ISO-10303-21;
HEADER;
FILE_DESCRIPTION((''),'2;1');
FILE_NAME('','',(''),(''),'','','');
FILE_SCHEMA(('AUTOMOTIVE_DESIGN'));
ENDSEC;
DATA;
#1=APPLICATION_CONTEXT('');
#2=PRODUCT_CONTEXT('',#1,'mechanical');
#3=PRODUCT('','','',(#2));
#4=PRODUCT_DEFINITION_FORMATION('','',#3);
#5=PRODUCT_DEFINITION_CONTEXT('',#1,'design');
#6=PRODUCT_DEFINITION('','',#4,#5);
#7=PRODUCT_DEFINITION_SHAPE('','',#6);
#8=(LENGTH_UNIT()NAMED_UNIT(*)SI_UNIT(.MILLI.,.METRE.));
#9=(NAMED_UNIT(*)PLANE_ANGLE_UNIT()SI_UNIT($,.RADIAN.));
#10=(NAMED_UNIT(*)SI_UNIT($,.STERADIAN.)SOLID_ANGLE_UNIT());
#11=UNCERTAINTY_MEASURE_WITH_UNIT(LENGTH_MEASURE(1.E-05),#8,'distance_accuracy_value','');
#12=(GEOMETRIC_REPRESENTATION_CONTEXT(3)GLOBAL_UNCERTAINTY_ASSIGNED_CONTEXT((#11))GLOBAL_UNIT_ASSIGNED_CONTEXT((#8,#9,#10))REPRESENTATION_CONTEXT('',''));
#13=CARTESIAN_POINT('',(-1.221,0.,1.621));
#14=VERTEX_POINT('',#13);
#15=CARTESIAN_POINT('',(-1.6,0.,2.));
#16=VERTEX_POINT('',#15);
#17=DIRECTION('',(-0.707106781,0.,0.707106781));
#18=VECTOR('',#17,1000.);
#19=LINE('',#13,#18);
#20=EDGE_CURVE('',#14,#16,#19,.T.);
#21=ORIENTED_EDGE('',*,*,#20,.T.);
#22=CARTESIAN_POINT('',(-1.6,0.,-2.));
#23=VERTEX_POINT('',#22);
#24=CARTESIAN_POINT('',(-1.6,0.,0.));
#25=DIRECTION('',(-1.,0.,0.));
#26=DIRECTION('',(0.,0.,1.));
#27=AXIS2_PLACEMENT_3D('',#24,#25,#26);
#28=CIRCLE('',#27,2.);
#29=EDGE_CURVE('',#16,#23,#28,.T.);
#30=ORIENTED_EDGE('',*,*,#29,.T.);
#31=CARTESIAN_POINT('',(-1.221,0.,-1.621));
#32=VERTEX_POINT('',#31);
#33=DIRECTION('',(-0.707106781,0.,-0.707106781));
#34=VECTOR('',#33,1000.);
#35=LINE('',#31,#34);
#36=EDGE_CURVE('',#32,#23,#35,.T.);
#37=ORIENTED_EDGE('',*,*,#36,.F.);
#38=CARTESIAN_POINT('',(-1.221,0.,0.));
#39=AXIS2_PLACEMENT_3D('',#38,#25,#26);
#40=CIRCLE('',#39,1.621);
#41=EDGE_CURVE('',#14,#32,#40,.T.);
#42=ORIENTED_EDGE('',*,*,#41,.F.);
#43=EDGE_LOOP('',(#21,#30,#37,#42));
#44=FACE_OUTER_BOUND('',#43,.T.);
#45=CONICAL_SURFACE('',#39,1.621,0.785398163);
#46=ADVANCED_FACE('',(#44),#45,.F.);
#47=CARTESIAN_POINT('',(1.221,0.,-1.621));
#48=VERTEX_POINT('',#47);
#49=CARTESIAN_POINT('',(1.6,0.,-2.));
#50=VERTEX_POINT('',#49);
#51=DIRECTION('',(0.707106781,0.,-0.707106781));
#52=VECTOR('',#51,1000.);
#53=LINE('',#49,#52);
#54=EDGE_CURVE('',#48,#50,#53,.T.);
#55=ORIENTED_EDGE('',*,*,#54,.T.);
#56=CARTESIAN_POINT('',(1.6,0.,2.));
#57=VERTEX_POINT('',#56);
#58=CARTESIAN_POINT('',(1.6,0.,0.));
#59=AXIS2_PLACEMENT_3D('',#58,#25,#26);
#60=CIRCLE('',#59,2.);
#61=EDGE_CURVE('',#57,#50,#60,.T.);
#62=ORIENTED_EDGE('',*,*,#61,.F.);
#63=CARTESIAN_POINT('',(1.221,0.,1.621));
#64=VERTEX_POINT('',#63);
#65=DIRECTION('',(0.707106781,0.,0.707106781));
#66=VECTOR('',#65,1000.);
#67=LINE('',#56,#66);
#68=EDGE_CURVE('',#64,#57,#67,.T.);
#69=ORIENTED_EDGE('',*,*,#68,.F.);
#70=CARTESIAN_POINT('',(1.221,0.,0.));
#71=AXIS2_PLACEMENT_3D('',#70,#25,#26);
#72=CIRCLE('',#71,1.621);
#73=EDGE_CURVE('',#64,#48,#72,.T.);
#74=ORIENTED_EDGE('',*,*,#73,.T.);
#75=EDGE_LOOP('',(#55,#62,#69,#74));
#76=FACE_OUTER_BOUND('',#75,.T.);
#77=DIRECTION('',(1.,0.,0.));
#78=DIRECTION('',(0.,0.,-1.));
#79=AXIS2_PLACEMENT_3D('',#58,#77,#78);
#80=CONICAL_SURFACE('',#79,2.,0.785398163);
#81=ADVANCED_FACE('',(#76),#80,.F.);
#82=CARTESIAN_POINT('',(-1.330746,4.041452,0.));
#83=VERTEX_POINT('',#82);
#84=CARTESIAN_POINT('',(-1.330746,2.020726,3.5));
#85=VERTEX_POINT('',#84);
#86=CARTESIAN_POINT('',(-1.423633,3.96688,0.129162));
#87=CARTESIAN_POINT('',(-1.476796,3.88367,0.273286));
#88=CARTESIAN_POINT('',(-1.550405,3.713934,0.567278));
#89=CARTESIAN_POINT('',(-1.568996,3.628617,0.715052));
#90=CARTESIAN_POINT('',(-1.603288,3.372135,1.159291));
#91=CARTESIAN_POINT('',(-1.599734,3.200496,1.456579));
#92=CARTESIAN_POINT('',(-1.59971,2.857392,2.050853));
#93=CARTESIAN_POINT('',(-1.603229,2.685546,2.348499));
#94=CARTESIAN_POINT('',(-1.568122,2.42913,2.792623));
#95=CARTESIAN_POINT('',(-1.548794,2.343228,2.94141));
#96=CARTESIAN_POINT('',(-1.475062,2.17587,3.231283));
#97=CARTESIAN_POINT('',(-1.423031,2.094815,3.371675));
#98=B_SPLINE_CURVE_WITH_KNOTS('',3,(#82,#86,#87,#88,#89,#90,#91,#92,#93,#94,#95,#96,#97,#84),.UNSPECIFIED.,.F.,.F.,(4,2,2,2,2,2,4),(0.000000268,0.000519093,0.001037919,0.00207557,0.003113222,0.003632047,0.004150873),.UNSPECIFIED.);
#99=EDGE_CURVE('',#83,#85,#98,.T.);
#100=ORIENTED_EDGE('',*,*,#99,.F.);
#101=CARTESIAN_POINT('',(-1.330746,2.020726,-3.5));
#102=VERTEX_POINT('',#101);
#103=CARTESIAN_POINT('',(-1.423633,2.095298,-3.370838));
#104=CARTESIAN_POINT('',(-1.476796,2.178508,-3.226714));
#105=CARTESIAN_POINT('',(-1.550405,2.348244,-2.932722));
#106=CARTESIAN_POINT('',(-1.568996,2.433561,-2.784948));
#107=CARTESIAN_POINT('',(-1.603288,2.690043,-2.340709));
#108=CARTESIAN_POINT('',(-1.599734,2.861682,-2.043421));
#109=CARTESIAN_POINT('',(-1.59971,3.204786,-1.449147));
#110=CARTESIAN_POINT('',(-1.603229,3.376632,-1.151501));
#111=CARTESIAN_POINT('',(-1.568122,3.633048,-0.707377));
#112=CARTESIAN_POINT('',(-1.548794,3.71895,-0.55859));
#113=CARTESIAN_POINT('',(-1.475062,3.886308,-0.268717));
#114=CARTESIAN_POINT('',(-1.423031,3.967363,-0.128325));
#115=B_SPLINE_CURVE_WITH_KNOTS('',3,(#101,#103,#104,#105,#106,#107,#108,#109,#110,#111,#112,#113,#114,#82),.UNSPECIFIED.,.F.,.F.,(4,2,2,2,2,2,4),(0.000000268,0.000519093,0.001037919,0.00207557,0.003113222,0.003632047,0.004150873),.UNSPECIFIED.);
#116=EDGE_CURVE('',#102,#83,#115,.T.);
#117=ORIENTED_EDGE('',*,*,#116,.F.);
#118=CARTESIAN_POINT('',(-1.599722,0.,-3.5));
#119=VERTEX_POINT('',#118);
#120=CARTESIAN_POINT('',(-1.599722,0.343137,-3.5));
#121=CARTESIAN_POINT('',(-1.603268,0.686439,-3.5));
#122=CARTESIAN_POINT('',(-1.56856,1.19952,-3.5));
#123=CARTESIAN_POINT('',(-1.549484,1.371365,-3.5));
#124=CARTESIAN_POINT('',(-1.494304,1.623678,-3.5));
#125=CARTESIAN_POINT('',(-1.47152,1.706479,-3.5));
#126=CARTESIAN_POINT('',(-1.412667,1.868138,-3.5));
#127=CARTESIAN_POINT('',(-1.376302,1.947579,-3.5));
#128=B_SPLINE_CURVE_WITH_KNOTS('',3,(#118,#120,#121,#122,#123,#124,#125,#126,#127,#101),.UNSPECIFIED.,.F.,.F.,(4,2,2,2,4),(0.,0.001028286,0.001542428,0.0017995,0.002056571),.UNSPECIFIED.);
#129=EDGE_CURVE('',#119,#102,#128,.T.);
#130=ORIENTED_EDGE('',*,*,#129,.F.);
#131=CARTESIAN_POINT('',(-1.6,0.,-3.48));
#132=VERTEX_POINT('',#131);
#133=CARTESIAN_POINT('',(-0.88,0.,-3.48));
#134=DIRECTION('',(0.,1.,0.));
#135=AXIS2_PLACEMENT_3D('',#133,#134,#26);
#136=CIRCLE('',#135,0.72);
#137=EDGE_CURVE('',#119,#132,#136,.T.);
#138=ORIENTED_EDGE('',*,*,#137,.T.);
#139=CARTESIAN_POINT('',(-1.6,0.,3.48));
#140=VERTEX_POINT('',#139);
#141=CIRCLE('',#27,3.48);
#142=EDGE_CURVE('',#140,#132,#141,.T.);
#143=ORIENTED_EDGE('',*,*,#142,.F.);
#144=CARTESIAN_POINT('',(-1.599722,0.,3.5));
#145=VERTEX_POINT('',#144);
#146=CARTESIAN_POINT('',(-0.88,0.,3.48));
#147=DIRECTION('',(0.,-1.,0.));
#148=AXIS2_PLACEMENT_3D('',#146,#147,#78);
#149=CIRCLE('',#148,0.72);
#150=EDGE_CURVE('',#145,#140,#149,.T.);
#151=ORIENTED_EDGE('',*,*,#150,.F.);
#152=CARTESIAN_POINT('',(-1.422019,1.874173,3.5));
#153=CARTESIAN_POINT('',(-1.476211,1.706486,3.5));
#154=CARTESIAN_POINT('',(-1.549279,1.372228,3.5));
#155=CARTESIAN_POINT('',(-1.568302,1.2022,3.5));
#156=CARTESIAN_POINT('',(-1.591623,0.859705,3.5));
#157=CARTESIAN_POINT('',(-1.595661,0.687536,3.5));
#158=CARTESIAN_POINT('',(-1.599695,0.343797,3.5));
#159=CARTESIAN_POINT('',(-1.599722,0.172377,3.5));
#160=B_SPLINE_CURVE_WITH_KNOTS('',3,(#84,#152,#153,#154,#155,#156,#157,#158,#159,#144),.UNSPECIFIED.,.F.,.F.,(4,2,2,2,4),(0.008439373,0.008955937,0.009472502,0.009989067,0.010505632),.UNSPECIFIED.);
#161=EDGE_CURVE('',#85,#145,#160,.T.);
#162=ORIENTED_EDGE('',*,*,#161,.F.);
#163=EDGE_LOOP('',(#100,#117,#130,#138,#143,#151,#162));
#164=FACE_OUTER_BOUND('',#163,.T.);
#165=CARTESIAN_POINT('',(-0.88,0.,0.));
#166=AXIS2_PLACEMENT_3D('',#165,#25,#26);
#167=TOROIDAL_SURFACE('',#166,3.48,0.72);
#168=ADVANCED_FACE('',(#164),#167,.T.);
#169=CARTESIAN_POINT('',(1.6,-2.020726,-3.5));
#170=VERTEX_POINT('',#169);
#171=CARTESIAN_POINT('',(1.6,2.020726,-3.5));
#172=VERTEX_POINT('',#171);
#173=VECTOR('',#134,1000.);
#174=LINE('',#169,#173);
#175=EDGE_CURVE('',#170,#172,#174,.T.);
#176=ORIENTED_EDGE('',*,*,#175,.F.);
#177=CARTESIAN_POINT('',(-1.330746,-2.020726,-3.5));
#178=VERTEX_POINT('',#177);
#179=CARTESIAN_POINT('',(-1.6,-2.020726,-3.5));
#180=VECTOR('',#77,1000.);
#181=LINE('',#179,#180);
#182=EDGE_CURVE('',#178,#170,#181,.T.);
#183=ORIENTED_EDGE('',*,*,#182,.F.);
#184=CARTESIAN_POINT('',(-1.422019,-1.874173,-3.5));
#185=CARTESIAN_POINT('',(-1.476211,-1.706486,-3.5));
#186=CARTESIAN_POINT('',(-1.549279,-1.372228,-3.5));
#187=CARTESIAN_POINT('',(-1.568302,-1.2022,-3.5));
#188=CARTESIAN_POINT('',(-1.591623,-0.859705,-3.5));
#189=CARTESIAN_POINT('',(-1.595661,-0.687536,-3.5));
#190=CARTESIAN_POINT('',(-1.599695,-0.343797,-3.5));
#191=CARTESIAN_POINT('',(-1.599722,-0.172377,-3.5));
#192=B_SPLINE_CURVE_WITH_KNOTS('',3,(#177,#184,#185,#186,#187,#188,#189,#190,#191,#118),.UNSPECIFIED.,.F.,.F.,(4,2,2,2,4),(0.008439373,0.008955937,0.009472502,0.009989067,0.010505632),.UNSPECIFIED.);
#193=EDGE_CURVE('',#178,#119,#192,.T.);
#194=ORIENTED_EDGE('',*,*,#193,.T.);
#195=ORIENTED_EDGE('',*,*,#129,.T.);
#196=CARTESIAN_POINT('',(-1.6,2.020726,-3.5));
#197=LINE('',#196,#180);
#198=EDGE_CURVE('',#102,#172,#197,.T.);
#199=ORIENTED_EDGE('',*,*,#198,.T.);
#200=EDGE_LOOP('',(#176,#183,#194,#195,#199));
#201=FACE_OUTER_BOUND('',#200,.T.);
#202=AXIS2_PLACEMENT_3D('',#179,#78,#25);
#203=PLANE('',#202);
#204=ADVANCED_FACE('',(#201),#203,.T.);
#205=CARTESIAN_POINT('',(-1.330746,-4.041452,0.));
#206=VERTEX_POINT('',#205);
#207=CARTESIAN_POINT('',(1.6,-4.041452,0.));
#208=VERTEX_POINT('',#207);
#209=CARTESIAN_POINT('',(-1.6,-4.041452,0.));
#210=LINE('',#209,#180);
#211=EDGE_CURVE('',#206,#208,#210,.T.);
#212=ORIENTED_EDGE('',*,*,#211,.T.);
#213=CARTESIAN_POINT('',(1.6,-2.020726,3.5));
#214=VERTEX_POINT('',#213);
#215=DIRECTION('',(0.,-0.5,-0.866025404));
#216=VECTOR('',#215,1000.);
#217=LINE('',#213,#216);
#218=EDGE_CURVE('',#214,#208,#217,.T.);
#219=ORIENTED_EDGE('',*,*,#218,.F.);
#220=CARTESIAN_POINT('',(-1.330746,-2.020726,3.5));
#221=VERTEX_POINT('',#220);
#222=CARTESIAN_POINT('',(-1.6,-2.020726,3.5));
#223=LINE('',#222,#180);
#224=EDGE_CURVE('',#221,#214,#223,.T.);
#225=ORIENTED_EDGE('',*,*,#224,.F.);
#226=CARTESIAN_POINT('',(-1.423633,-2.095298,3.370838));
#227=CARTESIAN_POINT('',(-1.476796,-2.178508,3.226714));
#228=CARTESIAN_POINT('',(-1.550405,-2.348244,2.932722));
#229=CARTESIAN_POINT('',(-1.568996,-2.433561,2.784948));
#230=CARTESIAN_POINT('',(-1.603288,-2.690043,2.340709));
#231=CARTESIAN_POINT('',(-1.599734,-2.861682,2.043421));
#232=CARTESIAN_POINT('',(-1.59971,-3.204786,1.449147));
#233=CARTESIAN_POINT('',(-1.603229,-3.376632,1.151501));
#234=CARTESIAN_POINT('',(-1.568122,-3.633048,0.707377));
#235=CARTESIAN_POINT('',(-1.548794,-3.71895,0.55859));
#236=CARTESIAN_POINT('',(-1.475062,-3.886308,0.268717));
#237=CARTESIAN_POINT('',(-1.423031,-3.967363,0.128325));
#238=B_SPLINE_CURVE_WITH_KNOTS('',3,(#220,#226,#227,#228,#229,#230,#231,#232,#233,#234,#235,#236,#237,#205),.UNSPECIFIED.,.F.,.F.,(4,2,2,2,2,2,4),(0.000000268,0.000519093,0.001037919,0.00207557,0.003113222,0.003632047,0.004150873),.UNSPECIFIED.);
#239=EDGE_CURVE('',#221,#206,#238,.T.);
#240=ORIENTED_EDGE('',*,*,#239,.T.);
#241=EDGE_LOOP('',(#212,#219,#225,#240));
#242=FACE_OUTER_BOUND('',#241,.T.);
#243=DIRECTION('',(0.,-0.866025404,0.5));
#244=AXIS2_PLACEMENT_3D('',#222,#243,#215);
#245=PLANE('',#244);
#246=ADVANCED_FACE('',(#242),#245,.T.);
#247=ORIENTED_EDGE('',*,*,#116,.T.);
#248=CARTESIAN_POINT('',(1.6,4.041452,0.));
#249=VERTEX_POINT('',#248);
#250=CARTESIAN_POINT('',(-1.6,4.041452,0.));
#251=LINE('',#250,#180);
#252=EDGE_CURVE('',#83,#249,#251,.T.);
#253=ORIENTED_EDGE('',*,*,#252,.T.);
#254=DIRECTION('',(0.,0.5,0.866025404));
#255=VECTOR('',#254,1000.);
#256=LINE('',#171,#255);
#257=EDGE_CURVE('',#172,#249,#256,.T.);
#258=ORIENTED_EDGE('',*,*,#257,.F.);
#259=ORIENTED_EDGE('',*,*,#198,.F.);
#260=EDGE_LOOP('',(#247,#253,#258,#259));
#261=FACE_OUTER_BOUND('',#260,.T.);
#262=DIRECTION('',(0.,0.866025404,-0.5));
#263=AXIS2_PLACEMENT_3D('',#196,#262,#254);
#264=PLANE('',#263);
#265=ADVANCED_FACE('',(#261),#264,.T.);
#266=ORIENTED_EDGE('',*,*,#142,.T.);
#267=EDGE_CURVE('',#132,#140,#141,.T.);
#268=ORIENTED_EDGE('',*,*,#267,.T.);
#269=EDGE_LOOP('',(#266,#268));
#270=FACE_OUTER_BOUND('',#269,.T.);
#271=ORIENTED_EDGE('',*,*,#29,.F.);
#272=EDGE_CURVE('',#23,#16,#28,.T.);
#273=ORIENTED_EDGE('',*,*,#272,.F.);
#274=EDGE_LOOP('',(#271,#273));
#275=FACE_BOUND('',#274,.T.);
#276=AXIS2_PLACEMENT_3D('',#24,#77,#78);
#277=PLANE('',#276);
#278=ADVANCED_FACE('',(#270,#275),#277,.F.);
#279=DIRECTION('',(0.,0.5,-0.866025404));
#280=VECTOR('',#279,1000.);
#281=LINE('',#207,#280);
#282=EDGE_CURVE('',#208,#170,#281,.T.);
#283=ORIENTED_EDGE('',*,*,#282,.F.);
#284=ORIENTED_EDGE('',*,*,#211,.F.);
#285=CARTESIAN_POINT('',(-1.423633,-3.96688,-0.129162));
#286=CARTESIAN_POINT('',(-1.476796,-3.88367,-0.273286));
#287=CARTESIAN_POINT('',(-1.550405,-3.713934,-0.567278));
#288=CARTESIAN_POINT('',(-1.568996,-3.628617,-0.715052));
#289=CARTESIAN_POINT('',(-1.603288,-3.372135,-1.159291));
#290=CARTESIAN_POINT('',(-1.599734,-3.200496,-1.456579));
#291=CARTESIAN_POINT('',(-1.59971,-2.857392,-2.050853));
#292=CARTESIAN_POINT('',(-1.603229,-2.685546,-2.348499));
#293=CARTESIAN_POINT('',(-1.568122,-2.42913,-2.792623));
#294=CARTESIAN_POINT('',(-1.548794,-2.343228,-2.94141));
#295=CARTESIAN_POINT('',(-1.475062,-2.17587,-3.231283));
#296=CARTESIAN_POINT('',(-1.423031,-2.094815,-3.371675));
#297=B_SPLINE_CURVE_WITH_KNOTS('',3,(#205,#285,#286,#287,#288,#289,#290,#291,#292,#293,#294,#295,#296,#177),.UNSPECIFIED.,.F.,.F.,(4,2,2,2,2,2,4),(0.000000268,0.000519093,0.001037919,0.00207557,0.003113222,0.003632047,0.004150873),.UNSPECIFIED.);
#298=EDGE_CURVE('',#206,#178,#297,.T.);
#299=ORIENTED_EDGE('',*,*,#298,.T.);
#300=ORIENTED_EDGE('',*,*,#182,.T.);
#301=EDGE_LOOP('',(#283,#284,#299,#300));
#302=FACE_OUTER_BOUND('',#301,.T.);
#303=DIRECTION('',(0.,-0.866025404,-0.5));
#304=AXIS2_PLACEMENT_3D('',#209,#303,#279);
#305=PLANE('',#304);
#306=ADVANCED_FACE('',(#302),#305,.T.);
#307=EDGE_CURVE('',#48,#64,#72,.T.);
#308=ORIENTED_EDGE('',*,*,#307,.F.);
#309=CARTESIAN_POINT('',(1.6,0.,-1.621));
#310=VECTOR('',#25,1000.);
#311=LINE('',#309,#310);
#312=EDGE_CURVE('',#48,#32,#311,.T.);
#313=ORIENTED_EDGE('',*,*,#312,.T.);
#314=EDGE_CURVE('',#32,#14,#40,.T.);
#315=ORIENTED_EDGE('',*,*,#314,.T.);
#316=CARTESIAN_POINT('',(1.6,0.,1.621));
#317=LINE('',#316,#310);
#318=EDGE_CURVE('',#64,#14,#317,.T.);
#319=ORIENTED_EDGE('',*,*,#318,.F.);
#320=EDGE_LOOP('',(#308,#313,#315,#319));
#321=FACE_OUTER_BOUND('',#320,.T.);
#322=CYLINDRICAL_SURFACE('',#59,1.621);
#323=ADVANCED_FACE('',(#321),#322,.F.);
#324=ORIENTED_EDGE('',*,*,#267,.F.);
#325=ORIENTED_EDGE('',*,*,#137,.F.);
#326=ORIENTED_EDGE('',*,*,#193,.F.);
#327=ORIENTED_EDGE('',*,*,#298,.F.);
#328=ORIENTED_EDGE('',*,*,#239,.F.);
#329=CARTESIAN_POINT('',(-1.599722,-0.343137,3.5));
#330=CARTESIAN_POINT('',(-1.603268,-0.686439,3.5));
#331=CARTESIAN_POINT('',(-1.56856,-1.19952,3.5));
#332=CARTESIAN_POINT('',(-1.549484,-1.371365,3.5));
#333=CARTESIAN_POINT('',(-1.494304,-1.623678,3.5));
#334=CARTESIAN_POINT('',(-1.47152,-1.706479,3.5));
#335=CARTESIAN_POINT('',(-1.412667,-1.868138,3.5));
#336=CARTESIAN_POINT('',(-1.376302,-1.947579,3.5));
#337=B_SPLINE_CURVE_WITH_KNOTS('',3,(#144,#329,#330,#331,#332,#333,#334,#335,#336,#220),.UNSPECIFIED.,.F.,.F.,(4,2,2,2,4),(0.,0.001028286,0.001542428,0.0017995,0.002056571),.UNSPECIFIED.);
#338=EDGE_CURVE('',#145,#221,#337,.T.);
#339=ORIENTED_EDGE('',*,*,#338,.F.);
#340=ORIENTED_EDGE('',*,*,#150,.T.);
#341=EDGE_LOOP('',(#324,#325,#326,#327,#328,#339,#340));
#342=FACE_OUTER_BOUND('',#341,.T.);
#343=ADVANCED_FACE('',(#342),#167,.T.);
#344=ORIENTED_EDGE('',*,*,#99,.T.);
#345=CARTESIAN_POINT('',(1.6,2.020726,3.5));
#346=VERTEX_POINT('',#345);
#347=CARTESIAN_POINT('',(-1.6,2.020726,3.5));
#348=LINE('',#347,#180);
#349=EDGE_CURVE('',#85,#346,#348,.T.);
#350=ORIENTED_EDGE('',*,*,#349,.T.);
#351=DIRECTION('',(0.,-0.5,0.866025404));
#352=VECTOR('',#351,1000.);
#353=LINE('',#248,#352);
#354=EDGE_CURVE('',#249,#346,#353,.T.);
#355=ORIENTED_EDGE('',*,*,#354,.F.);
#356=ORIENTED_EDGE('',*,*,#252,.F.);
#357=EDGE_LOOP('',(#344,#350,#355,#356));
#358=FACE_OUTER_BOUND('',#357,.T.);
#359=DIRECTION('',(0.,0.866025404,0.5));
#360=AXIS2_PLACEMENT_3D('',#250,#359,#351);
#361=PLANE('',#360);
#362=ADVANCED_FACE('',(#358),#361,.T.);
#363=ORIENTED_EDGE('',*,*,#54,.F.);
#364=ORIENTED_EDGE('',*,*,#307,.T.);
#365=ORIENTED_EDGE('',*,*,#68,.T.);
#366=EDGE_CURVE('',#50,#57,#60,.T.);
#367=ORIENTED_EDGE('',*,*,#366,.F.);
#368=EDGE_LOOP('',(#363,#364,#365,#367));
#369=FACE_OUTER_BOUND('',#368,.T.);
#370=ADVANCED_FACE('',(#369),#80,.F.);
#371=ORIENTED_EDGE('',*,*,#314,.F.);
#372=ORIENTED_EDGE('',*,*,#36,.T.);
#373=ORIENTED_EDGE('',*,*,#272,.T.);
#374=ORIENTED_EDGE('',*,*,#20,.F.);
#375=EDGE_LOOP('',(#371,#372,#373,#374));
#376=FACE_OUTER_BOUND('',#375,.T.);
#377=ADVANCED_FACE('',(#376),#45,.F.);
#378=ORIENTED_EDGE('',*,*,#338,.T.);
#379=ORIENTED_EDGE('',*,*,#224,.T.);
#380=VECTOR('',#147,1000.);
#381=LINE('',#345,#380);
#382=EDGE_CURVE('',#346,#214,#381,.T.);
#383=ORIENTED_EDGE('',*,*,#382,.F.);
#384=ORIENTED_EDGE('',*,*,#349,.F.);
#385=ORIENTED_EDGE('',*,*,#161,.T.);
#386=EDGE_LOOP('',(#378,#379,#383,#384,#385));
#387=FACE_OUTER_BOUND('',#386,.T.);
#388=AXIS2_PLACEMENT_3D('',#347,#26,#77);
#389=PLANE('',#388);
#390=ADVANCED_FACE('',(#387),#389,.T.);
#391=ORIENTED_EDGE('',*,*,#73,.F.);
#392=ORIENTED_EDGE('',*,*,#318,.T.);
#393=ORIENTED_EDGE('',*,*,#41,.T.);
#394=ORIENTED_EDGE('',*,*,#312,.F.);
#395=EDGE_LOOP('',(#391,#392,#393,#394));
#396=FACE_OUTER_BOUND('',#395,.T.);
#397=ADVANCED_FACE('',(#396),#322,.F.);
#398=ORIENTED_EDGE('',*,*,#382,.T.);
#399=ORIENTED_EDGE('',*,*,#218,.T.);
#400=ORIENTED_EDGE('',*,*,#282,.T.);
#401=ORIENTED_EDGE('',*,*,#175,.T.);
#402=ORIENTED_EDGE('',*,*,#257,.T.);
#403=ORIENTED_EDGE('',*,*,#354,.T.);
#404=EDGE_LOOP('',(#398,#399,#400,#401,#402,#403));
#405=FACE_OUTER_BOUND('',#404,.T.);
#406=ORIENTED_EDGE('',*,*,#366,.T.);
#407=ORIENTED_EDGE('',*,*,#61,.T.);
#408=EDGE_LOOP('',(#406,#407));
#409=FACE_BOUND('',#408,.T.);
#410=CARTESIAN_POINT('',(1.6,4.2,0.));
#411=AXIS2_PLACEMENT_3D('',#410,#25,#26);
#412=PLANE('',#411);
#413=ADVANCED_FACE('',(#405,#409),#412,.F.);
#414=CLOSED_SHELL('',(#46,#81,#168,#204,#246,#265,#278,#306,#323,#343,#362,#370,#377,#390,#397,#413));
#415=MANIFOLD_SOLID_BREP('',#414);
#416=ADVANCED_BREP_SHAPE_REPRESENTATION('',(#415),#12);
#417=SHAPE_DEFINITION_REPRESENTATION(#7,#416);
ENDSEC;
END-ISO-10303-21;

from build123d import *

# Parameters (mm, degrees)
CUT_EXTRUDE1_DEPTH      = 1.6
CUT_EXTRUDE1_DEPTH_BACK = 1.6
SKETCH3_W               = 14
SKETCH3_H               = 14


with BuildPart() as part:
    # Sketch1 → Revolve1 (revolve)
    with BuildSketch(Plane.XY, mode=Mode.PRIVATE) as revolve1_sk:
        with BuildLine():
            Line((-1.6, 0), (-1.6, 3.48))
            ThreePointArc((-1.6, 3.48), (-1.389116882, 3.989116882), (-0.88, 4.2))
            Line((-0.88, 4.2), (1.6, 4.2))
            Line((1.6, 4.2), (1.6, 0))
            Line((1.6, 0), (-1.6, 0))
        make_face()
    revolve(revolve1_sk.sketch.rotate(Axis((1.6, 0, 0), (-1, 0, 0)), 270), axis=Axis((1.6, 0, 0), (-1, 0, 0)))

    # Sketch2 → Cut-Revolve1 (revolve, cut)
    with BuildSketch(Plane.XY, mode=Mode.PRIVATE) as cut_revolve1_sk:
        Polygon((-1.6, 0), (-1.6, 2), (-1.221, 1.621), (1.221, 1.621), (1.6, 2), (1.6, 0), align=None)
    revolve(cut_revolve1_sk.sketch.rotate(Axis((1.6, 0, 0), (-1, 0, 0)), 270), axis=Axis((1.6, 0, 0), (-1, 0, 0)), mode=Mode.SUBTRACT)

    # Sketch3 → Cut-Extrude1 (cut, two sides: drawn at the far end of the back side and taken through both)
    with BuildSketch(Plane(origin=(0, 0, 0), x_dir=(0, 0, -1), z_dir=(1, 0, 0)).offset(-CUT_EXTRUDE1_DEPTH_BACK)):
        Rectangle(SKETCH3_W, SKETCH3_H)
        Polygon((-3.5, 2.020725942), (-3.5, -2.020725942), (0, -4.041451884), (3.5, -2.020725942), (3.5, 2.020725942), (0, 4.041451884), align=None, mode=Mode.SUBTRACT)
    extrude(amount=CUT_EXTRUDE1_DEPTH + CUT_EXTRUDE1_DEPTH_BACK, mode=Mode.SUBTRACT)


solid = part.part
